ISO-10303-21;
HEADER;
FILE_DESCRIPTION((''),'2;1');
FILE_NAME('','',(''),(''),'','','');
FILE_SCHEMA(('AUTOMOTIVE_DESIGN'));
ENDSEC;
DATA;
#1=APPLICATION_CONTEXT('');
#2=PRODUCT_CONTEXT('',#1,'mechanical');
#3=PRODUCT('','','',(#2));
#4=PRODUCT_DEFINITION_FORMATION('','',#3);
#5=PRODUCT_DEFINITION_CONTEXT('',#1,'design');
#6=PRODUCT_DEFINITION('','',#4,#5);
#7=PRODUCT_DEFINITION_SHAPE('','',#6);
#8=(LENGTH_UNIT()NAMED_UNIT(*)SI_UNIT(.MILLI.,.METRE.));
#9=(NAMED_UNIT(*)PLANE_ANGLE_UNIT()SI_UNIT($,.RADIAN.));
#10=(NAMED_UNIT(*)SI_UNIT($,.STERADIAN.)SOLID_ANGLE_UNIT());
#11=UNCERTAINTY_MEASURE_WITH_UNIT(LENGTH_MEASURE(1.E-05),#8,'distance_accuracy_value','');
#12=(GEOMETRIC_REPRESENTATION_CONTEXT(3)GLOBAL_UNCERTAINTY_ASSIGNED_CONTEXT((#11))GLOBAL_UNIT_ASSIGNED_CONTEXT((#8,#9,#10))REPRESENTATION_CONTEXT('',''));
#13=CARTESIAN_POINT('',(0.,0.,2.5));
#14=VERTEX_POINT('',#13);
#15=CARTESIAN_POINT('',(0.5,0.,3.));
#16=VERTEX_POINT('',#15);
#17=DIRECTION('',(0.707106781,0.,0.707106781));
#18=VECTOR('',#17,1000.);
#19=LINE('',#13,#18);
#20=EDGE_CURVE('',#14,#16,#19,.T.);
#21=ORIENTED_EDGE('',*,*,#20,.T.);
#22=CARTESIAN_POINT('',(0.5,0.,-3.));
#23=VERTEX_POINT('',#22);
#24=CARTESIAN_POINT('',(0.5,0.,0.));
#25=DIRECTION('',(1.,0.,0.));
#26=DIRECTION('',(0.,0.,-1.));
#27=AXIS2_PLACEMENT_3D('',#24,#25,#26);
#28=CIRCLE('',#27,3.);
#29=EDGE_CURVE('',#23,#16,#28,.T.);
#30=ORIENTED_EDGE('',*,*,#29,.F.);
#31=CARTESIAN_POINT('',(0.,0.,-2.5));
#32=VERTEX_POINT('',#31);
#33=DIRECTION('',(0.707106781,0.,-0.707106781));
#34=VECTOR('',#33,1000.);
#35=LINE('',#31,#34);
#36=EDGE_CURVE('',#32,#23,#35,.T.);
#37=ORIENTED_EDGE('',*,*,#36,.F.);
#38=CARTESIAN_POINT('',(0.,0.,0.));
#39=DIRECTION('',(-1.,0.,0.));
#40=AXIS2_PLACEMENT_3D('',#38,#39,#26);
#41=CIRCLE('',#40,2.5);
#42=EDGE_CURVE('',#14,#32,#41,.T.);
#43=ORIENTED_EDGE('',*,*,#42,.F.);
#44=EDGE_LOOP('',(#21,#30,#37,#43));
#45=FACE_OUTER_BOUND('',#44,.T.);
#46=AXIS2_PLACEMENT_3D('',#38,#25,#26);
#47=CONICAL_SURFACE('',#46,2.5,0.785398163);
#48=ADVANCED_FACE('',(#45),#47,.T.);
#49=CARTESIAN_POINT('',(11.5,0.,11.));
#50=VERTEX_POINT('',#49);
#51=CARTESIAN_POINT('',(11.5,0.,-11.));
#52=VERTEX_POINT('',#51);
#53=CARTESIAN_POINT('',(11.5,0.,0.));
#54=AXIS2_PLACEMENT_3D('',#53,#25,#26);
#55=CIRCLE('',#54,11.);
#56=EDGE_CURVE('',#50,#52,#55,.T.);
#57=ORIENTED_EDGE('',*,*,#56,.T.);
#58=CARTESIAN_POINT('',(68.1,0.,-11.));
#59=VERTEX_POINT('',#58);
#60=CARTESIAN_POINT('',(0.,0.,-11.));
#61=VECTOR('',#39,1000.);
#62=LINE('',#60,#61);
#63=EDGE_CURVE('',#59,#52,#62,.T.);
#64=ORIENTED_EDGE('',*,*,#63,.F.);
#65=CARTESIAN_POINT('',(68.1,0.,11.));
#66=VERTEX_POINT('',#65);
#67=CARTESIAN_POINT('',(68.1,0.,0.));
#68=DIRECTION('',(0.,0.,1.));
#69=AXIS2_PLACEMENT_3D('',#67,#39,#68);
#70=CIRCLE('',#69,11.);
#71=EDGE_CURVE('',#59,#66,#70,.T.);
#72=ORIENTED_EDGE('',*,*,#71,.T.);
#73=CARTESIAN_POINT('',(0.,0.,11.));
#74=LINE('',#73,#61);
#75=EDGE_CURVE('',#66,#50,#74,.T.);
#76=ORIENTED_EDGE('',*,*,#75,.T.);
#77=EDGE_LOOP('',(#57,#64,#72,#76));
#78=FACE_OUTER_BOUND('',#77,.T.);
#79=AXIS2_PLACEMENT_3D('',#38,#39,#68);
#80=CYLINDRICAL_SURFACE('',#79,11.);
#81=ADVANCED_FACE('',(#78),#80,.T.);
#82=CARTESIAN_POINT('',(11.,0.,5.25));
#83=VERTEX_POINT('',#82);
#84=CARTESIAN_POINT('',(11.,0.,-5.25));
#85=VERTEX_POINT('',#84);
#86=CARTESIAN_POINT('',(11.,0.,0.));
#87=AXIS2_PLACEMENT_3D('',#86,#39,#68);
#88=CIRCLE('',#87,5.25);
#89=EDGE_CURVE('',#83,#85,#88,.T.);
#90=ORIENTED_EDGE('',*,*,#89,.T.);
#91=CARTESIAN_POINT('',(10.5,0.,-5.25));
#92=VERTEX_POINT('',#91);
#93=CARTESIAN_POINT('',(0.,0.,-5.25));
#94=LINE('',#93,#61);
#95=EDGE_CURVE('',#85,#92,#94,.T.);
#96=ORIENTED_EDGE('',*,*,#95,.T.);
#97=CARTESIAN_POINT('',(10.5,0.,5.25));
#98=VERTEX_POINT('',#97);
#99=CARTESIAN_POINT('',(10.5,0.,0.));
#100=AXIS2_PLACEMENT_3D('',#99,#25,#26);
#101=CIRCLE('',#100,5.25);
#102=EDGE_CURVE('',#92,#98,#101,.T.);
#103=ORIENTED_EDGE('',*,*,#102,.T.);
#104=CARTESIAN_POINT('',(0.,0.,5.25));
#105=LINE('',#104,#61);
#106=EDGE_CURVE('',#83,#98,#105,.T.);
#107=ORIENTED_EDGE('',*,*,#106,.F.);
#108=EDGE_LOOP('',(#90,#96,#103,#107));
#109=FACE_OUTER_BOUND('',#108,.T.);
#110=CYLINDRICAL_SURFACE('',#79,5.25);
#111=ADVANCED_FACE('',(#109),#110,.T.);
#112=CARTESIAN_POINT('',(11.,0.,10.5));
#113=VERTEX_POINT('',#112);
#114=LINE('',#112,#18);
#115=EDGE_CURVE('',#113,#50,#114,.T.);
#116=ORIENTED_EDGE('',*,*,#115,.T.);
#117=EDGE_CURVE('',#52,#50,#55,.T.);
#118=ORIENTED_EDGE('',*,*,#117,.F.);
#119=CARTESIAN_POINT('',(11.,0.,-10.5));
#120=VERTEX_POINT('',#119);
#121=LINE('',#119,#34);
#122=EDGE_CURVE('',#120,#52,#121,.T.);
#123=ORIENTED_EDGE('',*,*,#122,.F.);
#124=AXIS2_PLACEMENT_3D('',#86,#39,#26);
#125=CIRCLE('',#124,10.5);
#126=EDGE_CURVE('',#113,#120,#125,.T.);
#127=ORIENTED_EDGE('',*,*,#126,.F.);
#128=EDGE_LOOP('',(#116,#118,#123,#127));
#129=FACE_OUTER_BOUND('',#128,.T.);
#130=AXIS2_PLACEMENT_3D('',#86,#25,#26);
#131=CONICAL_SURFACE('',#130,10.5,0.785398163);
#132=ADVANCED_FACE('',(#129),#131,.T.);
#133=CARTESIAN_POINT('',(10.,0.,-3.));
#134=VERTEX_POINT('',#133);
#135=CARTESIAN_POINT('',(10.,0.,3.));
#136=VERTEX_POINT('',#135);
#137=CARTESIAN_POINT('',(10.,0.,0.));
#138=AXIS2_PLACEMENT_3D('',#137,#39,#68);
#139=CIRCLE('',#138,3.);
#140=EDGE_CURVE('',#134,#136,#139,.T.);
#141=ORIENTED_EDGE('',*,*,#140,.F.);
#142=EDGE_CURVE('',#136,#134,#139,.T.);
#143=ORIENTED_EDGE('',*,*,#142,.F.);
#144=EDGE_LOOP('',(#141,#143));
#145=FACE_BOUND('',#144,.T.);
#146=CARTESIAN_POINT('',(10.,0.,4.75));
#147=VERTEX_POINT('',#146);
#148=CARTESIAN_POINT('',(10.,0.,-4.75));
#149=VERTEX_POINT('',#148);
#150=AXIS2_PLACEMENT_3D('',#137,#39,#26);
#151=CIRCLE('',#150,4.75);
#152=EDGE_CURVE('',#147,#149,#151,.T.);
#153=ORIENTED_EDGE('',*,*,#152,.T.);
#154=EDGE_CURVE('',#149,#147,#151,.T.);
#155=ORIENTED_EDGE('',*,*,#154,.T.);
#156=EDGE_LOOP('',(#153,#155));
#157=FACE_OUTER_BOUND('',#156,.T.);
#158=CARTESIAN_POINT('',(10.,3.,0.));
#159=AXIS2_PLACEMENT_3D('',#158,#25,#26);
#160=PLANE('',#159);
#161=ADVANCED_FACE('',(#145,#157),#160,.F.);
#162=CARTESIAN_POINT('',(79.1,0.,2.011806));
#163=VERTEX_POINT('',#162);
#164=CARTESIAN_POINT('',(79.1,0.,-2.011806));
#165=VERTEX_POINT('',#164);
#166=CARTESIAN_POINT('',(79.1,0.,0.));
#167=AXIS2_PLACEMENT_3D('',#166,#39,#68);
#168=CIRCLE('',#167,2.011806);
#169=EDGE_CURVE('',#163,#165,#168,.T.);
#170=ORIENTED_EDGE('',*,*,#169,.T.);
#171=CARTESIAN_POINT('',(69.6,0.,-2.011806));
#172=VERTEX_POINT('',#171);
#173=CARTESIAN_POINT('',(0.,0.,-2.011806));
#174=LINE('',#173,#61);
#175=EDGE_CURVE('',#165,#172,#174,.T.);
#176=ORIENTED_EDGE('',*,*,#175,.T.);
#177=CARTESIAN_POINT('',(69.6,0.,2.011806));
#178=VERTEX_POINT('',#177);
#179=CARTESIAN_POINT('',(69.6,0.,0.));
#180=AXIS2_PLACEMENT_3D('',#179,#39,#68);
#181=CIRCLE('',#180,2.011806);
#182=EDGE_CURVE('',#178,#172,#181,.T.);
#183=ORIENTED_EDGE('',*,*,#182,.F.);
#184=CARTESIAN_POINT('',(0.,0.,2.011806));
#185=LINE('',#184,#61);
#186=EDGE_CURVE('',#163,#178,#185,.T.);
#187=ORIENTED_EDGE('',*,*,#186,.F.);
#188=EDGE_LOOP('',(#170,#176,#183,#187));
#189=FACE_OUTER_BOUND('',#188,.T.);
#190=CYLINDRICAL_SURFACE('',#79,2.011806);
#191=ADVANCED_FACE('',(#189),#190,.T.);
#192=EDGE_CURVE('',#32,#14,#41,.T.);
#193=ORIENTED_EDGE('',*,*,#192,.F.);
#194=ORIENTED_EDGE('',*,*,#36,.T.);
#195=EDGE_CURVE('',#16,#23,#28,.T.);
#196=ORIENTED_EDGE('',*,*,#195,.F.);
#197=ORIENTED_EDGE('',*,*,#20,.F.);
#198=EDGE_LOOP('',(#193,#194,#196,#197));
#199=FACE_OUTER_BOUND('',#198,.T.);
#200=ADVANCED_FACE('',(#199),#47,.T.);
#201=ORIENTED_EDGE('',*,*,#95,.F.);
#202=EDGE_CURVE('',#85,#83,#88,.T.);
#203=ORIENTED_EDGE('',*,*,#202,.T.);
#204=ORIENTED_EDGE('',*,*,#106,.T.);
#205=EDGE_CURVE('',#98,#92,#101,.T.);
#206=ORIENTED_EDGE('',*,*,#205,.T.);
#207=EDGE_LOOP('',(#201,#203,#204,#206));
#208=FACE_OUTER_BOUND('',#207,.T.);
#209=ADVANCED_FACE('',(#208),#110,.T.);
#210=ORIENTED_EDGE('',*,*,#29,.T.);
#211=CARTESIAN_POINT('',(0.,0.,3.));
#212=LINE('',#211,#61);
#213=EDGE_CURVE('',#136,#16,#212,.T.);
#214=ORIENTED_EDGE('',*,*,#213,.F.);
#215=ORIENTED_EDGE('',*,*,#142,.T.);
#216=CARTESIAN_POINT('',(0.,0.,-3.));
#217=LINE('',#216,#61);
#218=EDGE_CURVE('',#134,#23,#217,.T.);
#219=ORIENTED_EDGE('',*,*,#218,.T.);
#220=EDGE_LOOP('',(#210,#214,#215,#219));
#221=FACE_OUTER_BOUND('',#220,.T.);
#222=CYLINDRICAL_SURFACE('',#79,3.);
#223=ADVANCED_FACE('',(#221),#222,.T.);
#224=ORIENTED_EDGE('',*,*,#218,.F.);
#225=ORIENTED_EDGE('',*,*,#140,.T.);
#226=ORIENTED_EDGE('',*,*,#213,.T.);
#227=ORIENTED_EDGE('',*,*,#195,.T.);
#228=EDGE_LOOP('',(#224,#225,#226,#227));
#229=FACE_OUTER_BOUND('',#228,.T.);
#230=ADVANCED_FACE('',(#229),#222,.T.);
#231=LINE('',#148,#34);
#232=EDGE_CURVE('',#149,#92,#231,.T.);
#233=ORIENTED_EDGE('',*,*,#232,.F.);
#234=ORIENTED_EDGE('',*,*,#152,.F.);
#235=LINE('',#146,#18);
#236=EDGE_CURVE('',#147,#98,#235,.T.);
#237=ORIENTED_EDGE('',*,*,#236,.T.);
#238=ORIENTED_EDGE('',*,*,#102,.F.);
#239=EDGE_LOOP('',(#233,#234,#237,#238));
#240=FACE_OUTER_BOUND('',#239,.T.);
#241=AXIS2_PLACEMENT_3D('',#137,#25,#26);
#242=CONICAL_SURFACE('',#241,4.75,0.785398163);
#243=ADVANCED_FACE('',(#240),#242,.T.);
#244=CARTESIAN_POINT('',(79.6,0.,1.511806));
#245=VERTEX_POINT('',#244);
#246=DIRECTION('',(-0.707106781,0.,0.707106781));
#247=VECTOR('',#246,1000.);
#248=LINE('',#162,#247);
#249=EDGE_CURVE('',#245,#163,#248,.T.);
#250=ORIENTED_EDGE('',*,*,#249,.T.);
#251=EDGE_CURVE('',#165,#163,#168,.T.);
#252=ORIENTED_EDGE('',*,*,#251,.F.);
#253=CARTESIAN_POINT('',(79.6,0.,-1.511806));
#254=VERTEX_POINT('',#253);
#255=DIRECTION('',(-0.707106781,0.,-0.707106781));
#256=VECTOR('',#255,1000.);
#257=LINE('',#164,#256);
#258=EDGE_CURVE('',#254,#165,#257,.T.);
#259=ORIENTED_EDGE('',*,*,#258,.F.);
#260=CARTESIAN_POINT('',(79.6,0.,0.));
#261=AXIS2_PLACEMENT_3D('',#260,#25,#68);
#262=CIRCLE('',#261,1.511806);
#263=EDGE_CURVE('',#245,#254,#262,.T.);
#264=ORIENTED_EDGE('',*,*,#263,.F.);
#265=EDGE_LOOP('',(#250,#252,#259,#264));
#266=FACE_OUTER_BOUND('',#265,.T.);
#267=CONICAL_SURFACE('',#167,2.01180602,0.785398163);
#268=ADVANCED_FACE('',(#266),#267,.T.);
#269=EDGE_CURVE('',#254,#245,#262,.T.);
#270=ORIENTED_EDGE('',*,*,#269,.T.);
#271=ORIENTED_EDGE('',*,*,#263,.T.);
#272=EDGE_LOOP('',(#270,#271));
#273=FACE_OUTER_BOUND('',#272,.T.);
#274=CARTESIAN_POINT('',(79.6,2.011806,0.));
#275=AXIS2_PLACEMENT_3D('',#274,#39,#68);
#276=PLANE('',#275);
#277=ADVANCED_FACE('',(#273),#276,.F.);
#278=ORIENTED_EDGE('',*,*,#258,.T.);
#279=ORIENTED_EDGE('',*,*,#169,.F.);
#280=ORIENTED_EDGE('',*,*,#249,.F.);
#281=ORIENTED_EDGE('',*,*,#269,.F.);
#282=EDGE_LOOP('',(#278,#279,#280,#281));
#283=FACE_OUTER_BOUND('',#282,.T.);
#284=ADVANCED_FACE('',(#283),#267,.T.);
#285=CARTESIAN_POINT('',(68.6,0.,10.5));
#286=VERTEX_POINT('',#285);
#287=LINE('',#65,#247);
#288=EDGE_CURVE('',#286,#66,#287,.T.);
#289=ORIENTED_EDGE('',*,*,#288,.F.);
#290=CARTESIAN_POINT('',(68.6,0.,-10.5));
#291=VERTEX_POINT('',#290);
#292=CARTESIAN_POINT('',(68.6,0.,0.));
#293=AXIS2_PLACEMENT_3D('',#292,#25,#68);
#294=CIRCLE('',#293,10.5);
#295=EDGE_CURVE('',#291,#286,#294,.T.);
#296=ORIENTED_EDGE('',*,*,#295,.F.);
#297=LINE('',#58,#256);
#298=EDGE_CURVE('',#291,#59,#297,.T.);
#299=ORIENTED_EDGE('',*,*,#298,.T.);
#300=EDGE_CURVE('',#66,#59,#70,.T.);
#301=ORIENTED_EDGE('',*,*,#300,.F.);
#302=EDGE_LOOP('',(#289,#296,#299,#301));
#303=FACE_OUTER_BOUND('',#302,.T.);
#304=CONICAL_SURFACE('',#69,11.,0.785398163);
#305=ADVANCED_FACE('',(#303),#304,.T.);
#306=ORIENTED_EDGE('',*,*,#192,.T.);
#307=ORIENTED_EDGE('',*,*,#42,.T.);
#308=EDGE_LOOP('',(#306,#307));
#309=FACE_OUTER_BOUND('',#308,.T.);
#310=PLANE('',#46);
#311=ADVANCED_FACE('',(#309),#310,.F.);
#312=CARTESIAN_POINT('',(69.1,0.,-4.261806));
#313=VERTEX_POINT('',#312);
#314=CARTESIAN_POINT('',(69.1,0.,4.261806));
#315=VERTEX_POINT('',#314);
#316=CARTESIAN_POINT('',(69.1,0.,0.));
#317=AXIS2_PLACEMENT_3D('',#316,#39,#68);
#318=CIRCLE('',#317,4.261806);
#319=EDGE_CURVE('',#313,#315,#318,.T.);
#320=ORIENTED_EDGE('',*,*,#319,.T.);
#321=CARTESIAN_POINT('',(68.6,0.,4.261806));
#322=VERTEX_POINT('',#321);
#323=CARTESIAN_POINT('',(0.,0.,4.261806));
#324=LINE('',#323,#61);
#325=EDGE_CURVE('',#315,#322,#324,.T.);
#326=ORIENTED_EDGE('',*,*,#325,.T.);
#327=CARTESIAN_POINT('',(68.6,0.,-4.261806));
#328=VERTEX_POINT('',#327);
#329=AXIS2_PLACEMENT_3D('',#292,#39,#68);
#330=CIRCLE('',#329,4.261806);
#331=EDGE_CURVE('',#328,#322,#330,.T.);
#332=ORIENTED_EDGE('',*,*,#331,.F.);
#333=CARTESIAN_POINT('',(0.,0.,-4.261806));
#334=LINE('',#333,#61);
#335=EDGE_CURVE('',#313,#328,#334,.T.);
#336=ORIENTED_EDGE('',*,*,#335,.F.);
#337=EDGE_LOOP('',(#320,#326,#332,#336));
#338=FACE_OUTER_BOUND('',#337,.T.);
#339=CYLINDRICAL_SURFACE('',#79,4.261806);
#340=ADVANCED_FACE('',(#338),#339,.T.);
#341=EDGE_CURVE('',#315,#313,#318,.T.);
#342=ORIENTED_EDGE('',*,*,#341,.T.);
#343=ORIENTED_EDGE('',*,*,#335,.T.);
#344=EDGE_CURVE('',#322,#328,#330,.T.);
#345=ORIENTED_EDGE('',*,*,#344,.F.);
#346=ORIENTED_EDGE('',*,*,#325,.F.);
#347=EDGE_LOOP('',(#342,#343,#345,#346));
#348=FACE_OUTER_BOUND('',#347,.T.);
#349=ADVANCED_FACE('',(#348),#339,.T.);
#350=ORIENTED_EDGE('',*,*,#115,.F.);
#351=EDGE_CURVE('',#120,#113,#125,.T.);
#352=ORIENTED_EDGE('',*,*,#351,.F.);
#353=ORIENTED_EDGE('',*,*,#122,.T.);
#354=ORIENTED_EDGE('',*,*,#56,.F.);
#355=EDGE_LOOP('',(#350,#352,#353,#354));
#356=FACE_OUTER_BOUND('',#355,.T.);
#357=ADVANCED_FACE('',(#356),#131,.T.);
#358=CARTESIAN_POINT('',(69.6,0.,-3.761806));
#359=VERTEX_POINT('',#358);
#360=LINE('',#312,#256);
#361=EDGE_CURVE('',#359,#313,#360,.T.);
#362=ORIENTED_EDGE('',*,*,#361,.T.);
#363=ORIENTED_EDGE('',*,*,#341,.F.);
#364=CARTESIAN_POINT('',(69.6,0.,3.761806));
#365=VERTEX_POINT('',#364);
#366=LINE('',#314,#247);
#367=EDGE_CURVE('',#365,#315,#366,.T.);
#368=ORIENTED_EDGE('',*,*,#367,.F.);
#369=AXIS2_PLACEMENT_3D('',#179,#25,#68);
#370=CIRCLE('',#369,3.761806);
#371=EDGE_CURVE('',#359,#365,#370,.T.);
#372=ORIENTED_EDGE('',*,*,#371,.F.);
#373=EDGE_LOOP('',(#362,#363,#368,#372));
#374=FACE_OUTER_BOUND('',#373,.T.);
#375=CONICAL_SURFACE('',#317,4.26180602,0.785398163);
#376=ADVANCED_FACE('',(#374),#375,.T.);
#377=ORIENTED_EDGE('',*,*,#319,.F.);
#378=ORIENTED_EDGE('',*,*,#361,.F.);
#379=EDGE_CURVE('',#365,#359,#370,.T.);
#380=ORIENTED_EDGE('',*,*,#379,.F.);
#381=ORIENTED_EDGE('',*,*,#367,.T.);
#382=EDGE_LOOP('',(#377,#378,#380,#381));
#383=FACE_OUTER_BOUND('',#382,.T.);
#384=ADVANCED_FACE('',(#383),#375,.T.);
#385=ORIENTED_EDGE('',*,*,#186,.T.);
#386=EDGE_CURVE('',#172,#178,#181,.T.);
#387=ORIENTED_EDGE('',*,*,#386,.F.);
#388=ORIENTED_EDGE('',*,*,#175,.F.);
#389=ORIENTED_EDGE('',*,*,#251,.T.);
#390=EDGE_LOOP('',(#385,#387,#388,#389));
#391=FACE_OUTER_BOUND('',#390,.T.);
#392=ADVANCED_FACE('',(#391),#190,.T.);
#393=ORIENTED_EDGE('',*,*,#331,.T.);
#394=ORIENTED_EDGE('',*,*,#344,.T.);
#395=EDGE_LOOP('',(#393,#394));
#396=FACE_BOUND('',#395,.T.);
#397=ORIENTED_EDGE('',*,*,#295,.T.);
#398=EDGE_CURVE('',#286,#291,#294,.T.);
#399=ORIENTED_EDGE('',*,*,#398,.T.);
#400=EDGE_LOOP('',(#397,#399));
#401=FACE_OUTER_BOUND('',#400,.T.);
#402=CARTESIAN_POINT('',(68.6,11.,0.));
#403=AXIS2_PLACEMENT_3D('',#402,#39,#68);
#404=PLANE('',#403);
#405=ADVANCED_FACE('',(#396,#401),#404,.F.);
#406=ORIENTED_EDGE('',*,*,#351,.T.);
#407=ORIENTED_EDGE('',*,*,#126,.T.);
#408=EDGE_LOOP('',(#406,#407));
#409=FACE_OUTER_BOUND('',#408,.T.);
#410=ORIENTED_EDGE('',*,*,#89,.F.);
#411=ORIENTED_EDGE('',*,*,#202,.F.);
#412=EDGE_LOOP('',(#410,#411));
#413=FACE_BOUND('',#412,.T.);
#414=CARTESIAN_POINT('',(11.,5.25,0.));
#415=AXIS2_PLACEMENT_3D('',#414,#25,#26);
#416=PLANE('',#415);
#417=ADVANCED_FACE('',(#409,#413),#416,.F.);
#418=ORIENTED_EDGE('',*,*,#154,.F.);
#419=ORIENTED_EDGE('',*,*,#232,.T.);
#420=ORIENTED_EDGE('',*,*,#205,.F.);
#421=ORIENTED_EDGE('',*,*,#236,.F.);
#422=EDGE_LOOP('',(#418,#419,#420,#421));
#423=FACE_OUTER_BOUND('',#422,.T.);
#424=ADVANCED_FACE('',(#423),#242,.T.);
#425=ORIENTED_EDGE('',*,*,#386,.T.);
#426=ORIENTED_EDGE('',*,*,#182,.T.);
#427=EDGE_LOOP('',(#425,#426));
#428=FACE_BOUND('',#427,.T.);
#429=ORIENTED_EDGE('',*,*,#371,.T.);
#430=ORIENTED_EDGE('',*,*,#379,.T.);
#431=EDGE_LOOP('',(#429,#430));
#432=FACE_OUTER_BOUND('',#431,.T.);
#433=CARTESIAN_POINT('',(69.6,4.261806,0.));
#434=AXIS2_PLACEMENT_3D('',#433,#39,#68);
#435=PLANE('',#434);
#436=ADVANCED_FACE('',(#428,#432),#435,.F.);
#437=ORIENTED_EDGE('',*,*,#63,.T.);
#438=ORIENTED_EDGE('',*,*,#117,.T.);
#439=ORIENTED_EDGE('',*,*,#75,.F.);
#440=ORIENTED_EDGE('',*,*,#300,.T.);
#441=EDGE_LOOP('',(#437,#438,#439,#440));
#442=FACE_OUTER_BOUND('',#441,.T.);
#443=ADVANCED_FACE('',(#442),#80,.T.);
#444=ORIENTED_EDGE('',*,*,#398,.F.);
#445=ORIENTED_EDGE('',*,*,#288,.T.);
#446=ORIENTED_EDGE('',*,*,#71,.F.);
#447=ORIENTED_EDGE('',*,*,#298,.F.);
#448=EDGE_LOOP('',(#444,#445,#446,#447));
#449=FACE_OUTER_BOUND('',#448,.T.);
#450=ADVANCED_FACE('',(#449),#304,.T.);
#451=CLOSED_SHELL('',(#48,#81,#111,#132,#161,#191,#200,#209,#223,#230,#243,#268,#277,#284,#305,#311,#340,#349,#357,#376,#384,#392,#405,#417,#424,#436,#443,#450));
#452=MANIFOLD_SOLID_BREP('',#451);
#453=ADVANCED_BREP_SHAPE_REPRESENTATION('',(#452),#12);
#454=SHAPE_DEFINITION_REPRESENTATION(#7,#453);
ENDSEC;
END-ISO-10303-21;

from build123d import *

# Parameters (mm, degrees)
CHAMFER1_SIZE = 0.5


with BuildPart() as part:
    # Sketch1 → Revolve1 (revolve)
    with BuildSketch(Plane.XY, mode=Mode.PRIVATE) as revolve1_sk:
        Polygon((0, 0), (0, 3), (10, 3), (10, 5.25), (11, 5.25), (11, 11), (68.6, 11), (68.6, 4.26180602), (69.6, 4.26180602), (69.6, 2.01180602), (79.6, 2.01180602), (79.6, 0), align=None)
    revolve(revolve1_sk.sketch.rotate(Axis((0, 0, 0), (1, 0, 0)), 90), axis=Axis((0, 0, 0), (1, 0, 0)))

    # Chamfer1
    chamfer1_edges = [part.edges().sort_by_distance(p)[0] for p in [
        (69.6, 0, -4.26180602),
        (68.6, 0, -11),
        (11, 0, -11),
        (10, 0, -5.25),
        (0, 0, -3),
        (79.6, 0, -2.01180602),
    ]]
    chamfer(chamfer1_edges, length=CHAMFER1_SIZE)


solid = part.part
